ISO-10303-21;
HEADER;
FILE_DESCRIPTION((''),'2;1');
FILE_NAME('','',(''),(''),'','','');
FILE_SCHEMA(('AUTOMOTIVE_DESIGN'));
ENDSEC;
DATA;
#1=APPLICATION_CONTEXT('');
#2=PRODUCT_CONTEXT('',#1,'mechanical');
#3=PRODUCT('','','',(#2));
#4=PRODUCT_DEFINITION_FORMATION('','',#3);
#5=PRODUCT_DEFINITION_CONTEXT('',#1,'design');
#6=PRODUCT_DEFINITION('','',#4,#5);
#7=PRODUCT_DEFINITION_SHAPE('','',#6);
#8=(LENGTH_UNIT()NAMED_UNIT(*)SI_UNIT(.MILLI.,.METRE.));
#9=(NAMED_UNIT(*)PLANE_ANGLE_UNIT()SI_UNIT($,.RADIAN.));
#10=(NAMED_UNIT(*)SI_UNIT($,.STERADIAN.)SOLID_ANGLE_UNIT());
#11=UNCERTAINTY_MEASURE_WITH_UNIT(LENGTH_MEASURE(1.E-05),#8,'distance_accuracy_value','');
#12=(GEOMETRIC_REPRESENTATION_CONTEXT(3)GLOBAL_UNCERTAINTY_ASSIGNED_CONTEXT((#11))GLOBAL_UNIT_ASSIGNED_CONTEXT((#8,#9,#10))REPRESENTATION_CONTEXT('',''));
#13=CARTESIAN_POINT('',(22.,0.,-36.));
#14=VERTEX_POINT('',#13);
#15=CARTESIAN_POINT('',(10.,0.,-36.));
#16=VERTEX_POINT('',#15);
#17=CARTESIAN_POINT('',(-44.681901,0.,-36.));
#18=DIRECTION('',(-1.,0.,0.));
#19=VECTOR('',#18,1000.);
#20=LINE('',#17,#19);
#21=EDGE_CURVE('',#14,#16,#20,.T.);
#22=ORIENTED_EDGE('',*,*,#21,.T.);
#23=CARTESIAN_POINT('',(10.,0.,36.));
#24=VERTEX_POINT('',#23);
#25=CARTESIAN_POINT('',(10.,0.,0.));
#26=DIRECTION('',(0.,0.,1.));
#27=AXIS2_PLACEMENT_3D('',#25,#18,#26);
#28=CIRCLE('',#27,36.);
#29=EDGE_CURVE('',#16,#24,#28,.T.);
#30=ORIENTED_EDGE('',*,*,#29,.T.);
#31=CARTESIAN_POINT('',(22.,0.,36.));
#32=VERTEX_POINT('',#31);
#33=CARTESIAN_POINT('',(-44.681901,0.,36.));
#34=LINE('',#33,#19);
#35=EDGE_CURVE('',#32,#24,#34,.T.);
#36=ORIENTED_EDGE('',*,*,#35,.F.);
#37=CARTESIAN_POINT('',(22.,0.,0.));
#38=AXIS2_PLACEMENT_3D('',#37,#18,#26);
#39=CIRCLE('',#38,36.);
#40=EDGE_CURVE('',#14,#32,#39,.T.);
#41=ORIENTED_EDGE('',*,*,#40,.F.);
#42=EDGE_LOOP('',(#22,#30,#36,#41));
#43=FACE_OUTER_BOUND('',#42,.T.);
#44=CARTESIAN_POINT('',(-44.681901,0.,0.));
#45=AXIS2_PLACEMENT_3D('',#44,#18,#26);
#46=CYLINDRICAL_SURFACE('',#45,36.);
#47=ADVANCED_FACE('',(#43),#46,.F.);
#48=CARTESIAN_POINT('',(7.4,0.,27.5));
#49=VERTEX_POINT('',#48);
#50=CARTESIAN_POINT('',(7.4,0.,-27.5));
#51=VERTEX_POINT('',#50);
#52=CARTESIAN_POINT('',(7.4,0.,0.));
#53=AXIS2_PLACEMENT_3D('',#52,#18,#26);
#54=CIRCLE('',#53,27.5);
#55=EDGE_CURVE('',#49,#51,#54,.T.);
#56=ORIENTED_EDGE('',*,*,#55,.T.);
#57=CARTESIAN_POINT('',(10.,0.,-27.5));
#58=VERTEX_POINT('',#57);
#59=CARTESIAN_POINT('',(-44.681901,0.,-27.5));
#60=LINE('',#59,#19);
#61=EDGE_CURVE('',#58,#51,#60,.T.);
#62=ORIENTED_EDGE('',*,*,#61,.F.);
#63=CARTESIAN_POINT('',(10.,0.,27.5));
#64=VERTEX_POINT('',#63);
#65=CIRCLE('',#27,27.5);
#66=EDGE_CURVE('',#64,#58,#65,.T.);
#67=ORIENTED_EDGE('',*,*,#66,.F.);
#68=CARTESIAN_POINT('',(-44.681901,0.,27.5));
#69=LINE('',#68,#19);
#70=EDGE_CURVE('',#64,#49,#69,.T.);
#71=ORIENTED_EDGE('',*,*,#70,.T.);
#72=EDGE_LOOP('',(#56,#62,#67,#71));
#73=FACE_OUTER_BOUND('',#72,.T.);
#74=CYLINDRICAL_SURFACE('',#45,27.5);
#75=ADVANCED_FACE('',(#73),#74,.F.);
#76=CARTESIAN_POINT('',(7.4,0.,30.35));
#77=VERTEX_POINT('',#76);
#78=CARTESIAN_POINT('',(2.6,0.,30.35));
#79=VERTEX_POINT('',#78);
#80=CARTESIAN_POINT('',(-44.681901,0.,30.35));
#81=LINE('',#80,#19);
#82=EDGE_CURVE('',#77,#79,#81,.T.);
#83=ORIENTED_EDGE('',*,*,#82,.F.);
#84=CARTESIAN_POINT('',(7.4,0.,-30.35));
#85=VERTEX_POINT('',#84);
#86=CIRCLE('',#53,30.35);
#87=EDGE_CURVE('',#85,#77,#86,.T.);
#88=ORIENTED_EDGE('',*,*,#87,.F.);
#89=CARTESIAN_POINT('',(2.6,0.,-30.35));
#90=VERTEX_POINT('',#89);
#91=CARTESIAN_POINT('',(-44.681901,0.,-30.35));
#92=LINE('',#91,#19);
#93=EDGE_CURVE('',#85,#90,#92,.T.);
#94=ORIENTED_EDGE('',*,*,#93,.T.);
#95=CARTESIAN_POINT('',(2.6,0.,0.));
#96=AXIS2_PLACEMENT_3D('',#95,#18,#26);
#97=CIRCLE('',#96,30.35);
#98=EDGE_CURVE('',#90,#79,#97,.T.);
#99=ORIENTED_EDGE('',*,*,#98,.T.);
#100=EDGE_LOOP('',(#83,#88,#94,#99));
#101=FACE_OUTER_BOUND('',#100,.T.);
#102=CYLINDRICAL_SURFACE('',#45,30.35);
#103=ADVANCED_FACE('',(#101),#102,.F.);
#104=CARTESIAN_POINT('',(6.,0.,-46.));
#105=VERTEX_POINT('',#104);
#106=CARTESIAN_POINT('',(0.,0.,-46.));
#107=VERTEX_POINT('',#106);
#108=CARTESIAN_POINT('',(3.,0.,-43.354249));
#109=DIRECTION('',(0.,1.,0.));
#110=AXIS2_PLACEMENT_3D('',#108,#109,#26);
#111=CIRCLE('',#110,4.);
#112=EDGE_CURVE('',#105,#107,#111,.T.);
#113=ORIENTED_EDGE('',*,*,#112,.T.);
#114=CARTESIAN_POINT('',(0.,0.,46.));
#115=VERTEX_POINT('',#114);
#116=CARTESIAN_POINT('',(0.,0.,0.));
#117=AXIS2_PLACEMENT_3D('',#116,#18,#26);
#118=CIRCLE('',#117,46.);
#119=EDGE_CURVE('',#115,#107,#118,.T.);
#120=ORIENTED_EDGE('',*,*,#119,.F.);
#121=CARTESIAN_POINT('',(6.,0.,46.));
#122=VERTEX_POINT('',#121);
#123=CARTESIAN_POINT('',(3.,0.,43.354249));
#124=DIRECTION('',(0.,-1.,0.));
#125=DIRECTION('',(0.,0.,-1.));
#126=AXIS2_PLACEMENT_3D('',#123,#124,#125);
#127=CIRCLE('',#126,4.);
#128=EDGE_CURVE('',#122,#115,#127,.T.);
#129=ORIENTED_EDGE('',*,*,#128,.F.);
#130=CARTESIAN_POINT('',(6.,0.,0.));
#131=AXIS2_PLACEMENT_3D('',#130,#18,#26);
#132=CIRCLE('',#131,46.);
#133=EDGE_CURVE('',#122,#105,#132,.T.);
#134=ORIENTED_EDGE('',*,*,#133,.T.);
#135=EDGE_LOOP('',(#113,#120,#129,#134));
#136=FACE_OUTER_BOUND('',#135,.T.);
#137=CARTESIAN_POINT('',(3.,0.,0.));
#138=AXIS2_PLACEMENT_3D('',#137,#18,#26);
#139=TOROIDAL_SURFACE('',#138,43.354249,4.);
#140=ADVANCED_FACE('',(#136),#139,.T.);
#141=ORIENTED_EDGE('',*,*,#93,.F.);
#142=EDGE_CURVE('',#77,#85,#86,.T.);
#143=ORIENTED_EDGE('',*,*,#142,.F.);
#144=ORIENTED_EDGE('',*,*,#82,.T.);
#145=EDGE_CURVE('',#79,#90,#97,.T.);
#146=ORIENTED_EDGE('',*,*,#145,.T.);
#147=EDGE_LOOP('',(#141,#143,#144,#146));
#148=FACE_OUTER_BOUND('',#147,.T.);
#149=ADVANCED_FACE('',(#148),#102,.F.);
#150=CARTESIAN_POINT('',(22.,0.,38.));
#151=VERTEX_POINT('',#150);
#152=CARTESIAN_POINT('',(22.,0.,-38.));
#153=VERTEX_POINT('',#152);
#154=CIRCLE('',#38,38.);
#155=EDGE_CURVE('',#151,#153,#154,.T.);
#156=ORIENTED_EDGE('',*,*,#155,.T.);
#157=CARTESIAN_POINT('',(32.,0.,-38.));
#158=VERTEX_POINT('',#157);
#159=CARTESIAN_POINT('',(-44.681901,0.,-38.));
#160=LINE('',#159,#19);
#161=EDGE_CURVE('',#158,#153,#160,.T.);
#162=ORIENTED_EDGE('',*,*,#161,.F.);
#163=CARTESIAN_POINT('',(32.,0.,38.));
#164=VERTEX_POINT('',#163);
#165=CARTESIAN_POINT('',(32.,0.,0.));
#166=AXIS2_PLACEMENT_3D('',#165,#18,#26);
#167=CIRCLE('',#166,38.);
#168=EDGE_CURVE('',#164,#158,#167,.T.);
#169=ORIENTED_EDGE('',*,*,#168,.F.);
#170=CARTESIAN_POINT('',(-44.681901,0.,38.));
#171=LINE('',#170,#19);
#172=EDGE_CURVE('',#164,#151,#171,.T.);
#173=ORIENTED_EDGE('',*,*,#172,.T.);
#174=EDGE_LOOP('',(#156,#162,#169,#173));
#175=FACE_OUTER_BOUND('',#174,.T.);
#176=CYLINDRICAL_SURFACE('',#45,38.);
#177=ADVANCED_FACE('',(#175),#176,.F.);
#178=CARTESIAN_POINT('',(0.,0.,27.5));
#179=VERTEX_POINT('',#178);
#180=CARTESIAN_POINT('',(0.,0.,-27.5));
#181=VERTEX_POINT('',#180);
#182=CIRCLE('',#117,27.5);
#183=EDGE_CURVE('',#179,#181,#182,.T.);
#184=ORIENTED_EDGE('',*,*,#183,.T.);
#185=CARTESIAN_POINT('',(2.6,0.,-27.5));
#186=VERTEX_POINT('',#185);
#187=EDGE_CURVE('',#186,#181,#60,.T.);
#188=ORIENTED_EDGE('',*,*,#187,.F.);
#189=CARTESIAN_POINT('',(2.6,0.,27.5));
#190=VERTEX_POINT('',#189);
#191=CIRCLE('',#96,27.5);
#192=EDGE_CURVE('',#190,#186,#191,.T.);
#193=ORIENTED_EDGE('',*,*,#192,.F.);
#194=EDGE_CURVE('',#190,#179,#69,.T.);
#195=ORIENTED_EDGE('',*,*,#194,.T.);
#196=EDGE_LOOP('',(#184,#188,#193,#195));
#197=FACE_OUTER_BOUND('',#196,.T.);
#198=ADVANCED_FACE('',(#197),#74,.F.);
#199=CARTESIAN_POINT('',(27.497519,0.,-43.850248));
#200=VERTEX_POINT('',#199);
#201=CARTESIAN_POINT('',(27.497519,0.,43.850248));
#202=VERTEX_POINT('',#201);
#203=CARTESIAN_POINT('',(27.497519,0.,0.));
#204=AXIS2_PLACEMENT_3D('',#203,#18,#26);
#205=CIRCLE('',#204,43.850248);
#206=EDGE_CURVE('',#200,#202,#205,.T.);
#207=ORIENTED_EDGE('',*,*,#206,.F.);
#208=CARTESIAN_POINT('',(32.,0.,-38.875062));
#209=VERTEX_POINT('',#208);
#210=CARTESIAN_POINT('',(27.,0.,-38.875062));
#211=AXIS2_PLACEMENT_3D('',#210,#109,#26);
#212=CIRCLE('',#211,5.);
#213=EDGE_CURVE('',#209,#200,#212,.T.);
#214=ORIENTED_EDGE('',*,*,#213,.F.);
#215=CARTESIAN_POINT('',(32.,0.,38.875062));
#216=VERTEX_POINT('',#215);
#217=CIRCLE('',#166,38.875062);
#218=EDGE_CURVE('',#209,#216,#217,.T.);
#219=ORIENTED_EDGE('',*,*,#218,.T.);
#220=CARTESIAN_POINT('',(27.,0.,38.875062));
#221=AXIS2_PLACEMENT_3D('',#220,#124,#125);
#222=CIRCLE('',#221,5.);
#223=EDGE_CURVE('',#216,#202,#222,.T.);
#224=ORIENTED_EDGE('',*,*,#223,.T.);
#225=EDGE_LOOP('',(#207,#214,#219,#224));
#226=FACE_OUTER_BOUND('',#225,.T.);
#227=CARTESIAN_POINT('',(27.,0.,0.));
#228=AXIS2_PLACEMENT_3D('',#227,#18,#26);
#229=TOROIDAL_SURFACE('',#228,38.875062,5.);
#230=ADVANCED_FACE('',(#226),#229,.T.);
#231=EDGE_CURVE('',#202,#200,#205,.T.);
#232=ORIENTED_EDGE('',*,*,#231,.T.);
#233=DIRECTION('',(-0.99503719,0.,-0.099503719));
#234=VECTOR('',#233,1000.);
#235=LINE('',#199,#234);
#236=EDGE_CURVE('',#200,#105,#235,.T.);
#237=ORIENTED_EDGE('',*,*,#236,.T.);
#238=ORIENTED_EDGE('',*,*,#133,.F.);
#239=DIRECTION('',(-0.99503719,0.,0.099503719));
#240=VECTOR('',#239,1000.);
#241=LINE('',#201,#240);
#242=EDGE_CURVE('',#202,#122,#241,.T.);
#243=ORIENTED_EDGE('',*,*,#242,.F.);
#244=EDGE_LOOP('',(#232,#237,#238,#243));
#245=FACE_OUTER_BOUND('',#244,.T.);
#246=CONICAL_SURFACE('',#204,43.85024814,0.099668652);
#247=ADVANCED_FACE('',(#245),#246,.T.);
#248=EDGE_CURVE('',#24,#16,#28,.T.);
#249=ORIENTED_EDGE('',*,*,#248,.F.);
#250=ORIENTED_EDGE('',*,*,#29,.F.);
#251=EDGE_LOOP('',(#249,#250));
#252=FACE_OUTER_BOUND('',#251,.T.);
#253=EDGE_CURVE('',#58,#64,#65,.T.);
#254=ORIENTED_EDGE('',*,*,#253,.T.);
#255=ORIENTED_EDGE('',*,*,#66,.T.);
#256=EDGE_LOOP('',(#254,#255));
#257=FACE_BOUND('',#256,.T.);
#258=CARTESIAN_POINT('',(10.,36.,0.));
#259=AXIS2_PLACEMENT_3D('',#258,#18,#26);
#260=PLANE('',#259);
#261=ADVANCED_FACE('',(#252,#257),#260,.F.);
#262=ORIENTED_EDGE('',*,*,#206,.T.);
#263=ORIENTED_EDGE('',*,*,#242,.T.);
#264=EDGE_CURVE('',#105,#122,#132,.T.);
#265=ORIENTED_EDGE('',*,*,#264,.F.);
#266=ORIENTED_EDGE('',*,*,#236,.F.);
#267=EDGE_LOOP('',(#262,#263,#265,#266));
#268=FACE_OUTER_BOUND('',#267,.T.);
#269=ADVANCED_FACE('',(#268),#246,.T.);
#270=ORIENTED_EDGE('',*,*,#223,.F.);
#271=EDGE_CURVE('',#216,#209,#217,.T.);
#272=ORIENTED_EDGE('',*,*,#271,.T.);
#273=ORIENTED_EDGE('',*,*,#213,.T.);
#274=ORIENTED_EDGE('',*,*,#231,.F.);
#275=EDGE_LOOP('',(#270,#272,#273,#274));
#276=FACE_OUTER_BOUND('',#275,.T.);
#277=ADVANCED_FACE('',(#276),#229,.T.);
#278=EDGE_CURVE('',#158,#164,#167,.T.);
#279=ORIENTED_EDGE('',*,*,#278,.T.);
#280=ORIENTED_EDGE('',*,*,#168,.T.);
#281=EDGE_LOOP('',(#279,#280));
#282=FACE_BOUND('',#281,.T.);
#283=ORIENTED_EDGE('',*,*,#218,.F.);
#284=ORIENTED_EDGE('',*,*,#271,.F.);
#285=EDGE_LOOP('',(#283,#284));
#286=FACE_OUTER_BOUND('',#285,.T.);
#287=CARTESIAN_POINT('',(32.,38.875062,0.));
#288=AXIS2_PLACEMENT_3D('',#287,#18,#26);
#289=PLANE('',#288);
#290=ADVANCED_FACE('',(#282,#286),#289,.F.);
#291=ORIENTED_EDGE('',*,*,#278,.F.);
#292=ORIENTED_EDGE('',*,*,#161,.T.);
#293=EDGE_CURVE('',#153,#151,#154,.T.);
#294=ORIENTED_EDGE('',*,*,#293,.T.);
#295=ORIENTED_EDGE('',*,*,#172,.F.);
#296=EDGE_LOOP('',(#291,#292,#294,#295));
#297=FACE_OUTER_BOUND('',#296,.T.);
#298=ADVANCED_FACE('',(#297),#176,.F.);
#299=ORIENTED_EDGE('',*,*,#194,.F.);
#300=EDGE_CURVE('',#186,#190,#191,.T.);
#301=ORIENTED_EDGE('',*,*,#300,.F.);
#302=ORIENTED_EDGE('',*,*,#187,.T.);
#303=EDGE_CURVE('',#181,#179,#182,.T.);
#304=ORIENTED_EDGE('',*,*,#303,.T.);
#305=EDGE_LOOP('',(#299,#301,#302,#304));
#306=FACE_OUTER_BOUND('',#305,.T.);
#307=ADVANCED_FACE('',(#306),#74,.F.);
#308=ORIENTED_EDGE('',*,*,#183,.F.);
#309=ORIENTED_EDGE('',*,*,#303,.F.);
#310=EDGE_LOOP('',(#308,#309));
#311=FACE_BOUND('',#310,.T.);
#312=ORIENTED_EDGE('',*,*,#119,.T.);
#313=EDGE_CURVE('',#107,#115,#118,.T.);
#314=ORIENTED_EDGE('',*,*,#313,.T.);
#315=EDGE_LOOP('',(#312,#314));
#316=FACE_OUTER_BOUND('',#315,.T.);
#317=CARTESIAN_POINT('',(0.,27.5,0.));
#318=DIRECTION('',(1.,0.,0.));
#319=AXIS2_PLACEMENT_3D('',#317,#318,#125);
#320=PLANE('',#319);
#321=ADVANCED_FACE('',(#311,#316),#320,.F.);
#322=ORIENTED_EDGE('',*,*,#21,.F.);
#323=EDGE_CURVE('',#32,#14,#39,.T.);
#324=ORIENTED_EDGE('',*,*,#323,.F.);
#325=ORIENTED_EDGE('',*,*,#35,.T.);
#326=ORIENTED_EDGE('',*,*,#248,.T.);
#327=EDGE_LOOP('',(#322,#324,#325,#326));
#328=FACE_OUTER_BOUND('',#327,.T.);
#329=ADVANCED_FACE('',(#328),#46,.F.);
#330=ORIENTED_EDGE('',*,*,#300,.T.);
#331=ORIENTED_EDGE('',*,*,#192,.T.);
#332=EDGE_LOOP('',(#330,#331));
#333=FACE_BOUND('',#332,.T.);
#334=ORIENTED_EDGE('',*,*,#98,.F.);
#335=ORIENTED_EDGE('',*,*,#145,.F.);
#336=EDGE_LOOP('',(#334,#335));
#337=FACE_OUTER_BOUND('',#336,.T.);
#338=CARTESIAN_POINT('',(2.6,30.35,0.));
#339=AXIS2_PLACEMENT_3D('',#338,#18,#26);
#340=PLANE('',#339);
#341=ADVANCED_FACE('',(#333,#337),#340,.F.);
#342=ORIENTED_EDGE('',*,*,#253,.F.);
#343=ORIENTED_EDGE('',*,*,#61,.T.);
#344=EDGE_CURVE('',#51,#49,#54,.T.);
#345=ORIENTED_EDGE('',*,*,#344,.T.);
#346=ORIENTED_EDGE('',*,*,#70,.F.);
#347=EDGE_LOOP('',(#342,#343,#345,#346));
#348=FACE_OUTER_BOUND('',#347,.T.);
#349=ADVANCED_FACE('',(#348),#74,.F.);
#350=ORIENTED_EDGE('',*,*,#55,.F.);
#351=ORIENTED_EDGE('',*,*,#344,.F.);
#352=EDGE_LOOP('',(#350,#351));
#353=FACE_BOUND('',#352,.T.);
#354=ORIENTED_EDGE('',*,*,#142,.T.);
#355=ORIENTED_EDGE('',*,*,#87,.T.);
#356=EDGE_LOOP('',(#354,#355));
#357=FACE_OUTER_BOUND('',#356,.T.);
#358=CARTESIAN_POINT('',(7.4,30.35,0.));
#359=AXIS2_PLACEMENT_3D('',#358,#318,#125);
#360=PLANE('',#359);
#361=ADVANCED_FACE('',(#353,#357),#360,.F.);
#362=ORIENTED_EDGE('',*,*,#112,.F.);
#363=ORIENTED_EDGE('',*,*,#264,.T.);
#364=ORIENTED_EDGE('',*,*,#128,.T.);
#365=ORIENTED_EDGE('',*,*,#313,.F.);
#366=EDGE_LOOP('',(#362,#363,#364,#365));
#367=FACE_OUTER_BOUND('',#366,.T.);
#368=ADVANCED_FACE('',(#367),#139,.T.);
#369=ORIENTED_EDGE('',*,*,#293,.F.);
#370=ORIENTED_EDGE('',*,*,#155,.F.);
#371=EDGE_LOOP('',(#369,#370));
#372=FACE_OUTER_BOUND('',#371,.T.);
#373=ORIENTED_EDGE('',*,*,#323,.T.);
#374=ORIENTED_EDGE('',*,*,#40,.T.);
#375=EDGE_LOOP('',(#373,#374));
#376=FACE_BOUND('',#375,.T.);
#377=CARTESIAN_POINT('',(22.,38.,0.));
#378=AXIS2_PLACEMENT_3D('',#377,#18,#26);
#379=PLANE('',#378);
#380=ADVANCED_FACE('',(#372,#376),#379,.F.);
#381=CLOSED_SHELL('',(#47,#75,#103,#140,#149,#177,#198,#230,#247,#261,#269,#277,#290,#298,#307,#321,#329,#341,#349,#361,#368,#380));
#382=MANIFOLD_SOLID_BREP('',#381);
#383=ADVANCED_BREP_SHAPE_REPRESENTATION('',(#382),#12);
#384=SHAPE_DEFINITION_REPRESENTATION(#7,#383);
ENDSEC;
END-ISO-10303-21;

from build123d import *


with BuildPart() as part:
    # Sketch1 → Revolve1 (revolve)
    with BuildSketch(Plane.XY, mode=Mode.PRIVATE) as revolve1_sk:
        with BuildLine():
            Line((0, 27.5), (0, 46))
            ThreePointArc((0, 46), (3, 47.354248689), (6, 46))
            Line((6, 46), (27.497518595, 43.85024814))
            ThreePointArc((27.497518595, 43.85024814), (30.707262668, 42.230088793), (32, 38.875062189))
            Line((32, 38.875062189), (32, 38))
            Line((32, 38), (22, 38))
            Line((22, 38), (22, 36))
            Line((22, 36), (10, 36))
            Line((10, 36), (10, 27.5))
            Line((10, 27.5), (7.4, 27.5))
            Line((7.4, 27.5), (7.4, 30.35))
            Line((7.4, 30.35), (2.6, 30.35))
            Line((2.6, 30.35), (2.6, 27.5))
            Line((2.6, 27.5), (0, 27.5))
        make_face()
    revolve(revolve1_sk.sketch.rotate(Axis((-44.681900546, 0, 0), (1, 0, 0)), 90), axis=Axis((-44.681900546, 0, 0), (1, 0, 0)))


solid = part.part
